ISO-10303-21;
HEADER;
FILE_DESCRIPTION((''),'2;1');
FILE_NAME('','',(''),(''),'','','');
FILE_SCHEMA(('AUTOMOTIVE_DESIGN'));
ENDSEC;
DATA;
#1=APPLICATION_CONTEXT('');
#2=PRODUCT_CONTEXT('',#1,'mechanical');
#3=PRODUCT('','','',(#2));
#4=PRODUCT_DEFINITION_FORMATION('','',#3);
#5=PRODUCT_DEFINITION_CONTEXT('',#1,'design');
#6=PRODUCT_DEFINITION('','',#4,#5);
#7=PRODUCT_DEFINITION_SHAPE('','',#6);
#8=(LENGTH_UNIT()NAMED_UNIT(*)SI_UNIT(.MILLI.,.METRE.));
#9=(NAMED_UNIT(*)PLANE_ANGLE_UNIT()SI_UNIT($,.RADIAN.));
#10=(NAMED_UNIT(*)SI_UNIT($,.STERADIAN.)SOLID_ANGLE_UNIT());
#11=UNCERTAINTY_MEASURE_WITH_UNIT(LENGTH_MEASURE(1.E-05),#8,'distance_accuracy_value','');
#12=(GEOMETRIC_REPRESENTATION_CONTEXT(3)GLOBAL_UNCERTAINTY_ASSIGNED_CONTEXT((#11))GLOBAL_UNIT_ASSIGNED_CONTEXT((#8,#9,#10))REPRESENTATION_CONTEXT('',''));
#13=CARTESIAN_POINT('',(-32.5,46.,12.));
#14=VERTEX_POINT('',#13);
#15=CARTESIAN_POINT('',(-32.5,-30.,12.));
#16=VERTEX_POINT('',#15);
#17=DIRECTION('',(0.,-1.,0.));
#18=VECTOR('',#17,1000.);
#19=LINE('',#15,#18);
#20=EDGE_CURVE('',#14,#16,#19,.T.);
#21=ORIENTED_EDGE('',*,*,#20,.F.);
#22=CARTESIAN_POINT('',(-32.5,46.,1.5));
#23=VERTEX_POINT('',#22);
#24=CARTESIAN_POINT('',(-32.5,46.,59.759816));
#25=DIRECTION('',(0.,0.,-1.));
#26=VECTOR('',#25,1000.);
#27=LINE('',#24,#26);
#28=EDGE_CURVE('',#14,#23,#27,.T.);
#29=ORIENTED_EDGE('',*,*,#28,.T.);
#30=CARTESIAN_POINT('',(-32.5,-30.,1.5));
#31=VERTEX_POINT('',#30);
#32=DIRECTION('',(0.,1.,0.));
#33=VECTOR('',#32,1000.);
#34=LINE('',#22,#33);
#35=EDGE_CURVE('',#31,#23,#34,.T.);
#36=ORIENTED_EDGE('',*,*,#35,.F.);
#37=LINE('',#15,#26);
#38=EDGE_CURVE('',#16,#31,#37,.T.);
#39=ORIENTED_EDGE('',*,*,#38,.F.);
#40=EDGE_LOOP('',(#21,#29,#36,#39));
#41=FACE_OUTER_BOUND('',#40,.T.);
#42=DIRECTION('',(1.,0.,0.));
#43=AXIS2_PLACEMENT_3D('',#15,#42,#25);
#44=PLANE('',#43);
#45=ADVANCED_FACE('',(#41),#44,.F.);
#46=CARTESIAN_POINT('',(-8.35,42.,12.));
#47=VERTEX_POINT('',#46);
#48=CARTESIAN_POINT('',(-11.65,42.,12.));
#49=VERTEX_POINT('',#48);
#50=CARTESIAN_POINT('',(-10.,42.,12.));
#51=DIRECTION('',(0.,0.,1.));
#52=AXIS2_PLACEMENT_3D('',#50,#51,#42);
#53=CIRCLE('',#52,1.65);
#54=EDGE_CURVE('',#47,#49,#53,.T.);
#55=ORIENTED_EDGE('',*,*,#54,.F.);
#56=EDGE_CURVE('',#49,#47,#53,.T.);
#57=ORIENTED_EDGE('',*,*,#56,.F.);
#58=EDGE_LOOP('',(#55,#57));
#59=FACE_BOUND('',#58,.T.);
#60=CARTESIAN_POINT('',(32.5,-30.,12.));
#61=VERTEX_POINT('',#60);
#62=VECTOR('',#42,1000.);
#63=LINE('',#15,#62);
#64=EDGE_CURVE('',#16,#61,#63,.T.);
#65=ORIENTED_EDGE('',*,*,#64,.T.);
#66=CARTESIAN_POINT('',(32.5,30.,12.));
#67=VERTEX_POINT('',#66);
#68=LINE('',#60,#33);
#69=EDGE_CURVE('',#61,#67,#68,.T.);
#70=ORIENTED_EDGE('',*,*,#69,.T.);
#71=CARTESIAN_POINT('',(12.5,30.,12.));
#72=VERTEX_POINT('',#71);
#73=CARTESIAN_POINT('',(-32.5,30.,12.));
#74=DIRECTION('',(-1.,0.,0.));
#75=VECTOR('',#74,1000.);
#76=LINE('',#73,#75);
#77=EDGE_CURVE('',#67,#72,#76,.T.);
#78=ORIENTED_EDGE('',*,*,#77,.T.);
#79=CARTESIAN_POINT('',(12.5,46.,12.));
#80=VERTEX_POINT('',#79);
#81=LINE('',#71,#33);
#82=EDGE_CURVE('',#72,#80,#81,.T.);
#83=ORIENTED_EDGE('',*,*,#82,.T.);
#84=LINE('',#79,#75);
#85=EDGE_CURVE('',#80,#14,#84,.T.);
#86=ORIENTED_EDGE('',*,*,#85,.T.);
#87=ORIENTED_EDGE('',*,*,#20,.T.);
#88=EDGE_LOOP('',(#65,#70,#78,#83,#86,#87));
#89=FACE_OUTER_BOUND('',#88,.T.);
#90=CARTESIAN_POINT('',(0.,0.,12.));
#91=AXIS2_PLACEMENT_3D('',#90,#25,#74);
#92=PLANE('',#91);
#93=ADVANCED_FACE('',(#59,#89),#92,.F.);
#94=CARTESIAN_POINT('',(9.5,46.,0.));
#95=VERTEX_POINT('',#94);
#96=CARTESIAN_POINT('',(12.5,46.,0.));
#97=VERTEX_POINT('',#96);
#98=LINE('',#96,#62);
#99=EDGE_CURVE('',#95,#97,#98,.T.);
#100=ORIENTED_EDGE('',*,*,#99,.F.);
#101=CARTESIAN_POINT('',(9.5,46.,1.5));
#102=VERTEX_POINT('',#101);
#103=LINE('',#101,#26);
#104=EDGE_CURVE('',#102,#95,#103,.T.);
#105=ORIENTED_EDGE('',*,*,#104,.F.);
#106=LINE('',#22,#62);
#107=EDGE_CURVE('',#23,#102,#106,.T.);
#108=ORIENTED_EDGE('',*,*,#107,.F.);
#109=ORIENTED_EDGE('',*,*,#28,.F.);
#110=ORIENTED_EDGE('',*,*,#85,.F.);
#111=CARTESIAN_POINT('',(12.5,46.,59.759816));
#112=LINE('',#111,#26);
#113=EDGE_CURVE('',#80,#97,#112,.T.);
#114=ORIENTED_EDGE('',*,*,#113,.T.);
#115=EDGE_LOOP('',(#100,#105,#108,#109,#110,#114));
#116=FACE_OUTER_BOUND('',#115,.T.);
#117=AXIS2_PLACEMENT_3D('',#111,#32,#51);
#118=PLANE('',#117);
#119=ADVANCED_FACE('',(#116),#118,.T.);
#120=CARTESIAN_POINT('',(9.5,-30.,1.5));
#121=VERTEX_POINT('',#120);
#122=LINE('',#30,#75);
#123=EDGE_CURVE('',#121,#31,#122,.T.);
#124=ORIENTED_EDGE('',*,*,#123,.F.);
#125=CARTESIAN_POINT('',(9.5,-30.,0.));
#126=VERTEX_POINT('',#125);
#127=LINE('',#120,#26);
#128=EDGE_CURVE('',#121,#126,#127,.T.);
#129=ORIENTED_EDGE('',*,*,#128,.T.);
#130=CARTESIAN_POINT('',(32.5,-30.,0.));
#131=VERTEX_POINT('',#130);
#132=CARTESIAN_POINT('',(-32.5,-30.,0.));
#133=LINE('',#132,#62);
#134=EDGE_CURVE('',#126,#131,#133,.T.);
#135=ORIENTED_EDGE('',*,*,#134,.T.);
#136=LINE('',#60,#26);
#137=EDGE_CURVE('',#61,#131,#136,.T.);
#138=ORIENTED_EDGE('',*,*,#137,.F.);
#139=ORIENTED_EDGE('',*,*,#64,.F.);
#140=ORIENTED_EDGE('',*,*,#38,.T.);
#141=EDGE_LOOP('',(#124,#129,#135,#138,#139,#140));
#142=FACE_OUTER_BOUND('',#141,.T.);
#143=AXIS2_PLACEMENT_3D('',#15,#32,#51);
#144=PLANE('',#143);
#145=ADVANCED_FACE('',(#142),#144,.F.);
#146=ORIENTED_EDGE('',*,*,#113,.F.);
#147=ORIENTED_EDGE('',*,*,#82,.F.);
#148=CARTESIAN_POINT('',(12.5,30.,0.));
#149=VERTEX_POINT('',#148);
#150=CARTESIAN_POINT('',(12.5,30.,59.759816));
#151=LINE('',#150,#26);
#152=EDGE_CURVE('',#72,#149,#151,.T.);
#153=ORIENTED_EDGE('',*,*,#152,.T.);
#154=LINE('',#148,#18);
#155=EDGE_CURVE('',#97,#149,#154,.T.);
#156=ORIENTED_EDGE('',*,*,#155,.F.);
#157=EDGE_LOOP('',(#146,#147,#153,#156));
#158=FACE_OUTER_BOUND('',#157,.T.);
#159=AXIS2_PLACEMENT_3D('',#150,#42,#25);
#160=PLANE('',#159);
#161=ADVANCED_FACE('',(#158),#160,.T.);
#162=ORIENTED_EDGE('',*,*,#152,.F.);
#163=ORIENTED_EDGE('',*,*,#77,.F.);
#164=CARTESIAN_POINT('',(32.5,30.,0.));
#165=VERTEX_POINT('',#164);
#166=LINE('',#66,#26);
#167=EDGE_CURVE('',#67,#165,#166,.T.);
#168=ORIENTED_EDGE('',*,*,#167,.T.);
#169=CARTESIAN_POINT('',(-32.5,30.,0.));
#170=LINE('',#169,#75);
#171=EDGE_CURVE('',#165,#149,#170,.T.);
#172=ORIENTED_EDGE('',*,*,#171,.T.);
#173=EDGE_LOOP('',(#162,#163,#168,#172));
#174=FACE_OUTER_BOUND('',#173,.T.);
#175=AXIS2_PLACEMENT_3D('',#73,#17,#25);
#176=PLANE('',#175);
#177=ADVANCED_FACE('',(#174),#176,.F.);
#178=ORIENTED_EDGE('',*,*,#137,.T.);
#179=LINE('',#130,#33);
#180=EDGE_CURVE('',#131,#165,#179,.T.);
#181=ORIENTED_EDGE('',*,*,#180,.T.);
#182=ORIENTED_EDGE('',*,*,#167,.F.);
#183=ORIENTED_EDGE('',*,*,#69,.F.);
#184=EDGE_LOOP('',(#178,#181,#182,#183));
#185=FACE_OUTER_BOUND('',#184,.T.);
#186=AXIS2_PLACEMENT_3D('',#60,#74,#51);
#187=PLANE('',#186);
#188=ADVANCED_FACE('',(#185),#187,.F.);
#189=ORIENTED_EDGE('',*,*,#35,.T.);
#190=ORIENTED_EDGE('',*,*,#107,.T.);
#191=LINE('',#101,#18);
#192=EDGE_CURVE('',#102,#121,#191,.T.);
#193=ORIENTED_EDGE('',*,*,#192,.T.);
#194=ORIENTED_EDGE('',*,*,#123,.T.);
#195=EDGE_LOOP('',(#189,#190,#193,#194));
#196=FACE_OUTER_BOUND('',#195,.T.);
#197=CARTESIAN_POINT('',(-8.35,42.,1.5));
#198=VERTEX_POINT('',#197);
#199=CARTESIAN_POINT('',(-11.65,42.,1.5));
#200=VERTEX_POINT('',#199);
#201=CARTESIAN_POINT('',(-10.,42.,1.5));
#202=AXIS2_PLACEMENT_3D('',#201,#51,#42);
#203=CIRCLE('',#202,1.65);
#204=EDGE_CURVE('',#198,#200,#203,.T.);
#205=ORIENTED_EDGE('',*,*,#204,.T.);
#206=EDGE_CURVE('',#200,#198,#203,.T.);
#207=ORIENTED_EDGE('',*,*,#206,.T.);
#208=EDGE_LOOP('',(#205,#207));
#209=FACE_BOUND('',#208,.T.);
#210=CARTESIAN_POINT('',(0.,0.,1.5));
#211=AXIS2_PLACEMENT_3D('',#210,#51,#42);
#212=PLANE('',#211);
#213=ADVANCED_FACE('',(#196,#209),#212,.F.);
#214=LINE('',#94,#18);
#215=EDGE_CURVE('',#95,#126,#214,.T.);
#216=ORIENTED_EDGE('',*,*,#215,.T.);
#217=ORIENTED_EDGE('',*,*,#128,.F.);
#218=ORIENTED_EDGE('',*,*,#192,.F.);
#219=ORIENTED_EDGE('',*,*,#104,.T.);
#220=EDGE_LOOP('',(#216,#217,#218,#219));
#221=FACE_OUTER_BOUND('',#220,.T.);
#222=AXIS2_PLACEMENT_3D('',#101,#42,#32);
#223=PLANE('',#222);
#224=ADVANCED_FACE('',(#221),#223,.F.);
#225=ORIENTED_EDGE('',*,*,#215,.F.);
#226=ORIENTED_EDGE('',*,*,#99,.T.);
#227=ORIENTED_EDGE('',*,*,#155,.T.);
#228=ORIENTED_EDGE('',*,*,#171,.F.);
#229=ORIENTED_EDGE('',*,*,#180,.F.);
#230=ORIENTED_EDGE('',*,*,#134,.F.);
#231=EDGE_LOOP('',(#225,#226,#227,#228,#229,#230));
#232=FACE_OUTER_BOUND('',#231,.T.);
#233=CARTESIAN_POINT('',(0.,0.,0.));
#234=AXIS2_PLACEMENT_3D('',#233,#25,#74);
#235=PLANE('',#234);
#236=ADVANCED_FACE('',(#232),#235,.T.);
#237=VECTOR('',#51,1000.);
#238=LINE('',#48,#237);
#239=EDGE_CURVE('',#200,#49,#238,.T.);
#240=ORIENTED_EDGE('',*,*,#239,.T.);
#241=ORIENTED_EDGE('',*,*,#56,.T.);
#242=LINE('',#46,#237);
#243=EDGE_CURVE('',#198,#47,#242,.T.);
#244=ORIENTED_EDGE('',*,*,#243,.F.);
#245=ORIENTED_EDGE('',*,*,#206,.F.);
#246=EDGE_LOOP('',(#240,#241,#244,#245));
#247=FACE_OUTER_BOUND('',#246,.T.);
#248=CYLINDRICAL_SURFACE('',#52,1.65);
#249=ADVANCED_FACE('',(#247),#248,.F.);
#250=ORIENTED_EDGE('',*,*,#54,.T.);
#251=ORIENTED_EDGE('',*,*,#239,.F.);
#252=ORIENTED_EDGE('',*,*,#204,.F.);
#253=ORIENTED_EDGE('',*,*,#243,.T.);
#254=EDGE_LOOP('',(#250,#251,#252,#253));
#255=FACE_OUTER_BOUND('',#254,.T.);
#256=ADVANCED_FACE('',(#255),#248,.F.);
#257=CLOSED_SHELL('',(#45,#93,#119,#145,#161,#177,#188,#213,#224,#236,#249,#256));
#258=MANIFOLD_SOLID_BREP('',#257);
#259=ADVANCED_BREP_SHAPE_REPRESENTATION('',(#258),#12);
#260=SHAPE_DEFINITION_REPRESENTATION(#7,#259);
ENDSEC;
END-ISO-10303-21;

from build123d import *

# Parameters (mm, degrees)
SKETCH_1_W          = 65
SKETCH_1_H          = 60
EXTRUDE_1_DEPTH     = 12
SKETCH_4_W          = 45
SKETCH_4_H          = 16
EXTRUDE_2_DEPTH     = 12
SKETCH_5_W          = 42
SKETCH_5_H          = 76
CUT_EXTRUDE_1_DEPTH = 1.5
HOLE_WIZARD_M4_1_D  = 3.3


with BuildPart() as part:
    # 草图1 → 凸台-拉伸1 (new body)
    with BuildSketch(Plane.XY):
        Rectangle(SKETCH_1_W, SKETCH_1_H)
    extrude(amount=EXTRUDE_1_DEPTH)

    # 草图4 → 凸台-拉伸2 (add)
    with BuildSketch(Plane(origin=(0, 0, 0), x_dir=(-1, 0, 0), z_dir=(0, 0, -1))):
        with Locations((10, 38)):
            Rectangle(SKETCH_4_W, SKETCH_4_H)
    extrude(amount=-EXTRUDE_2_DEPTH)

    # 草图5 → 切除-拉伸1 (cut)
    with BuildSketch(Plane(origin=(0, 0, 0), x_dir=(-1, 0, 0), z_dir=(0, 0, -1))):
        with Locations((11.5, 8)):
            Rectangle(SKETCH_5_W, SKETCH_5_H)
    extrude(amount=-CUT_EXTRUDE_1_DEPTH, mode=Mode.SUBTRACT)

    # M4 螺纹孔1 (through all)
    with Locations(Plane(origin=(-10, 42, 12), x_dir=(1, 0, 0), z_dir=(0, 0, 1))):
        with Locations((0, 0)):
            Hole(HOLE_WIZARD_M4_1_D / 2)


solid = part.part
